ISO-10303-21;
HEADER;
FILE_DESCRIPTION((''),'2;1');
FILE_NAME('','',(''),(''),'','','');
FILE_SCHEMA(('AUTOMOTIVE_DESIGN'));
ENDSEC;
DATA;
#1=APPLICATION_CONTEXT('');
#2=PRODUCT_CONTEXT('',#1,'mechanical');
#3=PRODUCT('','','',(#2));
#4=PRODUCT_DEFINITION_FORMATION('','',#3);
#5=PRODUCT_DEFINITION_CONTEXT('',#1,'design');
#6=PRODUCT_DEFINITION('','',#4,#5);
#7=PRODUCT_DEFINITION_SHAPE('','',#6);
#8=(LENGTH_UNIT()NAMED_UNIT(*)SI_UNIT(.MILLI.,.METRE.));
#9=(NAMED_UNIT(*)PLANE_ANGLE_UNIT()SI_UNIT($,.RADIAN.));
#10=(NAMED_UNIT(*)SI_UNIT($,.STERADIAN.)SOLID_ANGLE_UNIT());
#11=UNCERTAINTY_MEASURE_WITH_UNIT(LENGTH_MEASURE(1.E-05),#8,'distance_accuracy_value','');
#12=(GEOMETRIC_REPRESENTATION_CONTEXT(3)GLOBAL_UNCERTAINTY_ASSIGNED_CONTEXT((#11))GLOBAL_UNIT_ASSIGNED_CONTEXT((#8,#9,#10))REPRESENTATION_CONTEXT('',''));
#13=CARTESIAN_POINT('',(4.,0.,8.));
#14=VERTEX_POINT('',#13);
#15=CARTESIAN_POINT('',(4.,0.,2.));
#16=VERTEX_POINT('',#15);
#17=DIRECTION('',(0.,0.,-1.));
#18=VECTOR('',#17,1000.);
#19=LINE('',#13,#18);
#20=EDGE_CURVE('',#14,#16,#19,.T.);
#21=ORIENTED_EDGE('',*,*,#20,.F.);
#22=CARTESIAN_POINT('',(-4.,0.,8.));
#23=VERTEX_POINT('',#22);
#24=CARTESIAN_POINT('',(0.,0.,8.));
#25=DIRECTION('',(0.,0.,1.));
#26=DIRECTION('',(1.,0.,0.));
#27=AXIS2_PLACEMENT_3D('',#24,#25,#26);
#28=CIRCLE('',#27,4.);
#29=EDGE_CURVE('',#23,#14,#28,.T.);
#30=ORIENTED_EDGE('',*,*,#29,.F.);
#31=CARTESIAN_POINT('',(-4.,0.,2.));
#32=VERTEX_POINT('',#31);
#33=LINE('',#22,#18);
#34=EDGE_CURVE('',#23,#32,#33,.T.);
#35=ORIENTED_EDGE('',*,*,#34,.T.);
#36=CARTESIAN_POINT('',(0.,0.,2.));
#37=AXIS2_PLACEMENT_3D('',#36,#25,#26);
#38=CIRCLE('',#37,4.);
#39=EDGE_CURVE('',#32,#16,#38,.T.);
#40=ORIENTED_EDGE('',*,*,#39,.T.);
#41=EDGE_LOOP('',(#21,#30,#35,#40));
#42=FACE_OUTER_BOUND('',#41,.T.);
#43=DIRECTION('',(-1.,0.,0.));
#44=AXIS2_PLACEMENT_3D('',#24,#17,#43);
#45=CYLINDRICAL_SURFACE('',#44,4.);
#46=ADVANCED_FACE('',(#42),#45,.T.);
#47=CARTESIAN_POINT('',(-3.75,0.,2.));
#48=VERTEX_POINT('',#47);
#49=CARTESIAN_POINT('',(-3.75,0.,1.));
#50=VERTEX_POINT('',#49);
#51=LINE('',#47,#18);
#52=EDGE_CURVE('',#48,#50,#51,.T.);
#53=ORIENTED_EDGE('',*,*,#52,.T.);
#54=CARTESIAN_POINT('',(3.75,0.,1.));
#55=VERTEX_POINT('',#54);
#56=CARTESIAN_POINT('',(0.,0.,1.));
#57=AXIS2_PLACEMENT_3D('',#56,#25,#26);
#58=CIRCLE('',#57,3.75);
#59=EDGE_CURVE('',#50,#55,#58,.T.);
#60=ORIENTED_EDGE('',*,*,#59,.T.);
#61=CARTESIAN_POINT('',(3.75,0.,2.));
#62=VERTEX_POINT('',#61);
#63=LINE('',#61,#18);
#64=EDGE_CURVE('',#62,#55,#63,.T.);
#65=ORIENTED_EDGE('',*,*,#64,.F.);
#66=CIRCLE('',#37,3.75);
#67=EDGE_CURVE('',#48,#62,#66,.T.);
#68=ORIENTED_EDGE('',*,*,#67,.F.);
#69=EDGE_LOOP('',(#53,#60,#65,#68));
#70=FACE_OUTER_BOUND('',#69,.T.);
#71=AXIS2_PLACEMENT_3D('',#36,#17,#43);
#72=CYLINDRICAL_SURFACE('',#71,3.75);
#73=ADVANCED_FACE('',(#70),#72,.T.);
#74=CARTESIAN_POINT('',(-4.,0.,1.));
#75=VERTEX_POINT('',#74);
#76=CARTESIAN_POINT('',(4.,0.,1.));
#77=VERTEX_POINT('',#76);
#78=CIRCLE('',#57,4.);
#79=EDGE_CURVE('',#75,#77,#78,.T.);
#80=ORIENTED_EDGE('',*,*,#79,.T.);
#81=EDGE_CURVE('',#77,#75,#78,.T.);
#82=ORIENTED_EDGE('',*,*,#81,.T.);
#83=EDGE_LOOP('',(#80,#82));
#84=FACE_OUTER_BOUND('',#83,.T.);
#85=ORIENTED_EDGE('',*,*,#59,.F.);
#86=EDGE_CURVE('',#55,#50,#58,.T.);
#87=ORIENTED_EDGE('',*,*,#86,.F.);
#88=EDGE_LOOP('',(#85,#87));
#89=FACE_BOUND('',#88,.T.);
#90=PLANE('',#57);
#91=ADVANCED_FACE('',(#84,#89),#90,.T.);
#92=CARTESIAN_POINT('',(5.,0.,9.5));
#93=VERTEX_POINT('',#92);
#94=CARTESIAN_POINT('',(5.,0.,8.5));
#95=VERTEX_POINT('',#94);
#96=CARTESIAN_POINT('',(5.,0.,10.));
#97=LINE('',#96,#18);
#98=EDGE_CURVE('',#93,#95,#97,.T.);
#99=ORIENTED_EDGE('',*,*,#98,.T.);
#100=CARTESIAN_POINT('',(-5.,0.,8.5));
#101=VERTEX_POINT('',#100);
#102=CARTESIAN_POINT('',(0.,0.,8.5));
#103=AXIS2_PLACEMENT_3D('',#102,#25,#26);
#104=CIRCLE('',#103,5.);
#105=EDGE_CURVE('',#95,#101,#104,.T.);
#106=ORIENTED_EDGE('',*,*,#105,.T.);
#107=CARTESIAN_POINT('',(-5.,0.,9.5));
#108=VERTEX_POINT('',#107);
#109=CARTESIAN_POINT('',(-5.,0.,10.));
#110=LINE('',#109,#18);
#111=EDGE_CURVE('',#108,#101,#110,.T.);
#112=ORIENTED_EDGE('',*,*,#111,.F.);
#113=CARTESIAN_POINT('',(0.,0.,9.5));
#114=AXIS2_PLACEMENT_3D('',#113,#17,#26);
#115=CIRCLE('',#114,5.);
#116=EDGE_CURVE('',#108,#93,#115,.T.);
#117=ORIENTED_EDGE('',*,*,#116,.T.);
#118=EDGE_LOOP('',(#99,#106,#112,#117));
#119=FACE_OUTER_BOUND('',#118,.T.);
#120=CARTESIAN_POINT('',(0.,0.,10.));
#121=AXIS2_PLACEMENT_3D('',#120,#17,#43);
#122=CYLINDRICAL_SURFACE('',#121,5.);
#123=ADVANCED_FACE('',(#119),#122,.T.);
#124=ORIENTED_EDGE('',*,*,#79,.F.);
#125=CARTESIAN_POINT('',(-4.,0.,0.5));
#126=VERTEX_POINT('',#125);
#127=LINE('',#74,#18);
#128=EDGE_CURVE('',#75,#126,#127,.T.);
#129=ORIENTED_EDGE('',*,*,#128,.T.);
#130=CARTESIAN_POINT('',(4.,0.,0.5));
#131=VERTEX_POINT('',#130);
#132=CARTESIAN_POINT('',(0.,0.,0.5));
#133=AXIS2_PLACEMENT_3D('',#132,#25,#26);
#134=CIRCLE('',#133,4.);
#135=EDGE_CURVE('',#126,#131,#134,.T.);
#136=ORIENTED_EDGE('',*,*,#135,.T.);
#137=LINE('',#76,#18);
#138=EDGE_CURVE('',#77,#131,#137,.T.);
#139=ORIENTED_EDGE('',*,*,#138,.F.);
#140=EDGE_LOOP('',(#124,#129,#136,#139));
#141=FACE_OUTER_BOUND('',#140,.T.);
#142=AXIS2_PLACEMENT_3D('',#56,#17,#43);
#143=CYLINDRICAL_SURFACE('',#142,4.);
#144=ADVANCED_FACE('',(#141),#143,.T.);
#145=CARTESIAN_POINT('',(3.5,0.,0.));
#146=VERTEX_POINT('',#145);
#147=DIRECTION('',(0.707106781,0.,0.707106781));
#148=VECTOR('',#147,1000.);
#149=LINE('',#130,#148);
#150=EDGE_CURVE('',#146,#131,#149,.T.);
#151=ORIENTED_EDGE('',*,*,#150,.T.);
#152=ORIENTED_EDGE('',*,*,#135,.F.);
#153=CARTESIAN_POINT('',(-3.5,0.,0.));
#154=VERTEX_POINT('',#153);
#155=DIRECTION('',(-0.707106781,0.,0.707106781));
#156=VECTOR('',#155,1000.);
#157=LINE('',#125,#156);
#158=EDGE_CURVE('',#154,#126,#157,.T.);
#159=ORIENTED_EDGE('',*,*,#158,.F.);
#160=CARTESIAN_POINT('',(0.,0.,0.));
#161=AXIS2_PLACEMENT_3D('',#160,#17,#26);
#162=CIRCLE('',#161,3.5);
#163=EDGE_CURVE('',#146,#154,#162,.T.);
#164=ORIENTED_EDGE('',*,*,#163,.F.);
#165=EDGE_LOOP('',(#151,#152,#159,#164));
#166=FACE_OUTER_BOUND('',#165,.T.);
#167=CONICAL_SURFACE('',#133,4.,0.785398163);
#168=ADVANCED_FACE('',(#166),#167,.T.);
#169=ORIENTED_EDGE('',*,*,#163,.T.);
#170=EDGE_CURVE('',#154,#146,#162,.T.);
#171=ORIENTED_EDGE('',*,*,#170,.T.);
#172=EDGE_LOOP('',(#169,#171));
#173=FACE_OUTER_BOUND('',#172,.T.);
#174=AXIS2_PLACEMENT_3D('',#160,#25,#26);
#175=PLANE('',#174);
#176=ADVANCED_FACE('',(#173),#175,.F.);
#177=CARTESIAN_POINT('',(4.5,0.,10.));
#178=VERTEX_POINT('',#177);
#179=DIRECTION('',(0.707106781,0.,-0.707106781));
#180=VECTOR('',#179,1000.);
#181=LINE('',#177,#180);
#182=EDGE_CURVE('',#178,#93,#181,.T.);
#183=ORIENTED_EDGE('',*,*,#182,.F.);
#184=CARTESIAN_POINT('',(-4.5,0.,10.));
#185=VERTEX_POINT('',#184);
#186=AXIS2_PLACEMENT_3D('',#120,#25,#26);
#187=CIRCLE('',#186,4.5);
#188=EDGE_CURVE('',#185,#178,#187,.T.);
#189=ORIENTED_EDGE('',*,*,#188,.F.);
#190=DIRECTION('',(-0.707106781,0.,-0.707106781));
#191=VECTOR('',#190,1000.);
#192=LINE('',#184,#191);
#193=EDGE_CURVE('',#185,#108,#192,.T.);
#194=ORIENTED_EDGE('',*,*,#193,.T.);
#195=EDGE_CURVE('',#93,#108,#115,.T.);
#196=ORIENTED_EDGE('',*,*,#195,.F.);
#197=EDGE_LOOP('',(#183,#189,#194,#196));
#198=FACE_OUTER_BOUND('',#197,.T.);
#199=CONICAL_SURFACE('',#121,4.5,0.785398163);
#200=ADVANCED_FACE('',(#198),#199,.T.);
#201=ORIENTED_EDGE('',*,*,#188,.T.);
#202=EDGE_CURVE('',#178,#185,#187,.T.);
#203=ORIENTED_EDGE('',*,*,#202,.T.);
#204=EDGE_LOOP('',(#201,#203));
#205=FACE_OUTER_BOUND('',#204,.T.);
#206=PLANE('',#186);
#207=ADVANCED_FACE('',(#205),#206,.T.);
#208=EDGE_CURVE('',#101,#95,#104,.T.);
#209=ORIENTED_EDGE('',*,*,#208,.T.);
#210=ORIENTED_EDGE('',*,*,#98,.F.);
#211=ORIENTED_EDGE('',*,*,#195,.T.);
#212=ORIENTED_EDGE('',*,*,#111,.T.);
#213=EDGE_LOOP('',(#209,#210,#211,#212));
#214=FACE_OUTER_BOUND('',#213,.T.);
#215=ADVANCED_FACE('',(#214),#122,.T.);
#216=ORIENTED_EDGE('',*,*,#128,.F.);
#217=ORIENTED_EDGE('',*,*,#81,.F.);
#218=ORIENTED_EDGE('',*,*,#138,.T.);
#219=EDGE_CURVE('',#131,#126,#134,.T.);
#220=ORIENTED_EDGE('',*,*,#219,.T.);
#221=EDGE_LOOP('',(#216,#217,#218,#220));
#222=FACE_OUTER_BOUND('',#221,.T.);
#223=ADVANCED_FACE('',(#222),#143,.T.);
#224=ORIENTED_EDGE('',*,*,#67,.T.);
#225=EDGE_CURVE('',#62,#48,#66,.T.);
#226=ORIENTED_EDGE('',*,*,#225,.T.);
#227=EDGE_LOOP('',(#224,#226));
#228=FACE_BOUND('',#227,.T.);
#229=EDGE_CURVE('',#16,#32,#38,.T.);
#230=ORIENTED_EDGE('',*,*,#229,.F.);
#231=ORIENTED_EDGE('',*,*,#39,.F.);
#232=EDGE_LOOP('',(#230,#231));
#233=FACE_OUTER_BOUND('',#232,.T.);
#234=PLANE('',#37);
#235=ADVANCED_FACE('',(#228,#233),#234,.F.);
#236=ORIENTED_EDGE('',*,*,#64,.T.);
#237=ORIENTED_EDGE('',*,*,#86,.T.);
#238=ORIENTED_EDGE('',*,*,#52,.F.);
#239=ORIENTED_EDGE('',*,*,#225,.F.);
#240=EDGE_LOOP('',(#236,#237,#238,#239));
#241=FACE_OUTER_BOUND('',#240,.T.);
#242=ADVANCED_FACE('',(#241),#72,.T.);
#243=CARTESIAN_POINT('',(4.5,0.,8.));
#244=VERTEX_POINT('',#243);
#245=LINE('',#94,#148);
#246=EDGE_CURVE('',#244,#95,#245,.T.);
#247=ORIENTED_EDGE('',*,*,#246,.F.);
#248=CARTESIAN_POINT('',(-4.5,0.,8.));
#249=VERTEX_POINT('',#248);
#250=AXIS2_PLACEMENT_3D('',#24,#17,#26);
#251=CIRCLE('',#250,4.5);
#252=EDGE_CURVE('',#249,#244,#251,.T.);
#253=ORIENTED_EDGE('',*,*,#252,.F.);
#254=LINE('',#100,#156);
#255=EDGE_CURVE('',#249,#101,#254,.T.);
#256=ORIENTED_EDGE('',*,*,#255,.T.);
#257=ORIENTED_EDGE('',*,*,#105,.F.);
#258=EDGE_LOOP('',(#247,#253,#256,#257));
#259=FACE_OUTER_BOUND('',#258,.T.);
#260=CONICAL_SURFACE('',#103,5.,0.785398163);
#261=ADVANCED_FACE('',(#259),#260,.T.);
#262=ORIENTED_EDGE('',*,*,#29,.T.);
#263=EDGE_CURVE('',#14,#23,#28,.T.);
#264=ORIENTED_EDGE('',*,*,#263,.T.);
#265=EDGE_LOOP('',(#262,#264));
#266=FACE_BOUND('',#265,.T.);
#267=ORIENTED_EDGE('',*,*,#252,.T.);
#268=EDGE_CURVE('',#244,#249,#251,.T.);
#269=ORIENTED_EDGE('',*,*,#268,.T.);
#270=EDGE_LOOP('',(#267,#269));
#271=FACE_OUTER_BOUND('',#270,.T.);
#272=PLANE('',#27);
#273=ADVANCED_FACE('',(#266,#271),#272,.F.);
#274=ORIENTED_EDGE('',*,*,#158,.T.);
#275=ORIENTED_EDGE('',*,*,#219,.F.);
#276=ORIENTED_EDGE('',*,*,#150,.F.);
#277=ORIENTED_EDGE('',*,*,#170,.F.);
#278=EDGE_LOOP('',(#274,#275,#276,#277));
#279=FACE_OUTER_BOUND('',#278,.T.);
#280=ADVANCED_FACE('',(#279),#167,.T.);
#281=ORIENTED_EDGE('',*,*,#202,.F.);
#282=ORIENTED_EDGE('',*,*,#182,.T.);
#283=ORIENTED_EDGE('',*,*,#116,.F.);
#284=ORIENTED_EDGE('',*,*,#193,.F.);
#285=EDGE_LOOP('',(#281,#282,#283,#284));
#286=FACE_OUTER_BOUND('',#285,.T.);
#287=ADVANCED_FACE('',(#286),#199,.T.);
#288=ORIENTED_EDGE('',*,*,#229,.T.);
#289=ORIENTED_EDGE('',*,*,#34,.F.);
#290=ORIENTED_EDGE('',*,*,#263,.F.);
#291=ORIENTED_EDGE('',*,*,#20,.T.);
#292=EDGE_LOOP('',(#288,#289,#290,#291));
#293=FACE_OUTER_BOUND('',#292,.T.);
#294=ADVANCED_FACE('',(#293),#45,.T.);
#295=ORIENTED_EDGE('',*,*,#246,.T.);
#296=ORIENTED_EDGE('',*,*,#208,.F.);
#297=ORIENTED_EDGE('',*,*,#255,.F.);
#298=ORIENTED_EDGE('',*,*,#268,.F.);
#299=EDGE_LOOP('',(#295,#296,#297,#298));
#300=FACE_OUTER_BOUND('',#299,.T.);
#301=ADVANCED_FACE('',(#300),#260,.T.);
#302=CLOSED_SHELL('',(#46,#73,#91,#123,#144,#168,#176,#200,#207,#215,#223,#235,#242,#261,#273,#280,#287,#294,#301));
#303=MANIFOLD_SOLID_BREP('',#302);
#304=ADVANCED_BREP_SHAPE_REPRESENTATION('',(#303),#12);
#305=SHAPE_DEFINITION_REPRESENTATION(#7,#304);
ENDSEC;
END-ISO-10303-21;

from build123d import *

# Parameters (mm, degrees)
SKETCH1_R           = 4
BOSS_EXTRUDE1_DEPTH = 1
SKETCH2_R           = 3.75
BOSS_EXTRUDE2_DEPTH = 1
SKETCH3_R           = 4
BOSS_EXTRUDE3_DEPTH = 6
SKETCH4_R           = 5
BOSS_EXTRUDE4_DEPTH = 2
CHAMFER1_SIZE       = 0.5


with BuildPart() as part:
    # Sketch1 → Boss-Extrude1 (new body)
    with BuildSketch(Plane.XY):
        Circle(SKETCH1_R)
    extrude(amount=BOSS_EXTRUDE1_DEPTH)

    # Sketch2 → Boss-Extrude2 (add)
    with BuildSketch(Plane.XY.offset(1)):
        Circle(SKETCH2_R)
    extrude(amount=BOSS_EXTRUDE2_DEPTH)

    # Sketch3 → Boss-Extrude3 (add)
    with BuildSketch(Plane.XY.offset(2)):
        Circle(SKETCH3_R)
    extrude(amount=BOSS_EXTRUDE3_DEPTH)

    # Sketch4 → Boss-Extrude4 (add)
    with BuildSketch(Plane.XY.offset(8)):
        Circle(SKETCH4_R)
    extrude(amount=BOSS_EXTRUDE4_DEPTH)

    # Chamfer1
    chamfer1_edges = [part.edges().sort_by_distance(p)[0] for p in [
        (-5, 0, 8),
        (-5, 0, 10),
        (-4, 0, 0),
    ]]
    chamfer(chamfer1_edges, length=CHAMFER1_SIZE)


solid = part.part
